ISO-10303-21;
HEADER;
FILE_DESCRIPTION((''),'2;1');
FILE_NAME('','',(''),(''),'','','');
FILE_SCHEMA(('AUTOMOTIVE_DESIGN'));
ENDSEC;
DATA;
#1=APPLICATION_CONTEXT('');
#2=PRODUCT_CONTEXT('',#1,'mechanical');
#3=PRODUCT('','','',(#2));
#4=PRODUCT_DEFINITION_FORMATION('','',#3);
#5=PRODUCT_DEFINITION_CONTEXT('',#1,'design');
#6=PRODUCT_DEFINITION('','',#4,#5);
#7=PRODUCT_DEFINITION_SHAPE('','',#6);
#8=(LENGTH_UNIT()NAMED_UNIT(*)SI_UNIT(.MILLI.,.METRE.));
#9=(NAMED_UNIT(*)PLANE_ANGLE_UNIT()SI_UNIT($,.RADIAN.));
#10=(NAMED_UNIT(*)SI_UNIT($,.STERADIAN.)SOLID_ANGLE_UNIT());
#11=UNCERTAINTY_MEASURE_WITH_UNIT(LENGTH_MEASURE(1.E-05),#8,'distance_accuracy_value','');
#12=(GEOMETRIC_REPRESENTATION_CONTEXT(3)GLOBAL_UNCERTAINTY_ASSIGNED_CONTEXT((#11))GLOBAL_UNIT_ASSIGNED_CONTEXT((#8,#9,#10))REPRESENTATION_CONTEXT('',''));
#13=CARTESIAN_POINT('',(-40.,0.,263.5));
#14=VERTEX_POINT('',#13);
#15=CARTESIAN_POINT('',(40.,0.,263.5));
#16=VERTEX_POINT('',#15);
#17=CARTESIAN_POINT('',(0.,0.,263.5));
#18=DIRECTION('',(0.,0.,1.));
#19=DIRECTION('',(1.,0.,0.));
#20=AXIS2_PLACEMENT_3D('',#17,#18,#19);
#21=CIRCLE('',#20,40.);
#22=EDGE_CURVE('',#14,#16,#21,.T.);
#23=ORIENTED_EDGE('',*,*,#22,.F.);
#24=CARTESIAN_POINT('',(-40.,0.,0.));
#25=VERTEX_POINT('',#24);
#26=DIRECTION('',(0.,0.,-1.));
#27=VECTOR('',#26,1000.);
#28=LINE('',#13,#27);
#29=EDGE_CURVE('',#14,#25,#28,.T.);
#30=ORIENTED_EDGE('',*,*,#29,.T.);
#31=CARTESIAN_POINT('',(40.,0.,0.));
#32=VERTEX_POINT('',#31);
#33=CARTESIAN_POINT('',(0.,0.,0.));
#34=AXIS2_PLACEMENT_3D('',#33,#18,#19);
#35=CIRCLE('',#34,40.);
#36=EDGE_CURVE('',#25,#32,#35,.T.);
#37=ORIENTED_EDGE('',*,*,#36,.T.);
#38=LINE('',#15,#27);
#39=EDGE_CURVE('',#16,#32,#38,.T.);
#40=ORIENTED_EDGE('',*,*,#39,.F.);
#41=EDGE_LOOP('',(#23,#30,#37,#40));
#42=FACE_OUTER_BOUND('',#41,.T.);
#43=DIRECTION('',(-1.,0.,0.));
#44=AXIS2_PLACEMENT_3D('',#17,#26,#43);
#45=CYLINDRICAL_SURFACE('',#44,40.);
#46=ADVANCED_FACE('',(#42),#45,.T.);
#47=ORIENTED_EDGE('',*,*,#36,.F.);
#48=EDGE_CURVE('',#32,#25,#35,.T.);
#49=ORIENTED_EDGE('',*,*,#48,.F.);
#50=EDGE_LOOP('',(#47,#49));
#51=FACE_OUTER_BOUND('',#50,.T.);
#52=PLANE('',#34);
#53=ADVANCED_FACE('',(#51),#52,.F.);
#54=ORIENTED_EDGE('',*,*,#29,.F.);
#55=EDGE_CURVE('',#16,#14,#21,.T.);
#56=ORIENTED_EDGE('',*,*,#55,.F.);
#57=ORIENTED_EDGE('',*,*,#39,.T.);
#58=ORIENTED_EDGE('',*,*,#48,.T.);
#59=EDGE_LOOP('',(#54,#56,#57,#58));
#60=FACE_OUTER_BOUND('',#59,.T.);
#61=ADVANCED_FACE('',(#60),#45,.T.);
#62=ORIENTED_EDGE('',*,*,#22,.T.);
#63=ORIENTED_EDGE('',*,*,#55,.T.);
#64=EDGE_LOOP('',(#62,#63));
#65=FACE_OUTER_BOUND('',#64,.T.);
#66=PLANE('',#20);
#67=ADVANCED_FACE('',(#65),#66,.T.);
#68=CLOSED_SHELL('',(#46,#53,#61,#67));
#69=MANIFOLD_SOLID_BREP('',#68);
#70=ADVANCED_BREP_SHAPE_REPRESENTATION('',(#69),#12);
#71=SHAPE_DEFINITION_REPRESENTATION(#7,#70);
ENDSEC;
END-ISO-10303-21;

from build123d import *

# Parameters (mm, degrees)
SKETCH1_R           = 40
BOSS_EXTRUDE1_DEPTH = 263.5


with BuildPart() as part:
    # Sketch1 → Boss-Extrude1 (new body)
    with BuildSketch(Plane.XY):
        Circle(SKETCH1_R)
    extrude(amount=BOSS_EXTRUDE1_DEPTH)


solid = part.part
